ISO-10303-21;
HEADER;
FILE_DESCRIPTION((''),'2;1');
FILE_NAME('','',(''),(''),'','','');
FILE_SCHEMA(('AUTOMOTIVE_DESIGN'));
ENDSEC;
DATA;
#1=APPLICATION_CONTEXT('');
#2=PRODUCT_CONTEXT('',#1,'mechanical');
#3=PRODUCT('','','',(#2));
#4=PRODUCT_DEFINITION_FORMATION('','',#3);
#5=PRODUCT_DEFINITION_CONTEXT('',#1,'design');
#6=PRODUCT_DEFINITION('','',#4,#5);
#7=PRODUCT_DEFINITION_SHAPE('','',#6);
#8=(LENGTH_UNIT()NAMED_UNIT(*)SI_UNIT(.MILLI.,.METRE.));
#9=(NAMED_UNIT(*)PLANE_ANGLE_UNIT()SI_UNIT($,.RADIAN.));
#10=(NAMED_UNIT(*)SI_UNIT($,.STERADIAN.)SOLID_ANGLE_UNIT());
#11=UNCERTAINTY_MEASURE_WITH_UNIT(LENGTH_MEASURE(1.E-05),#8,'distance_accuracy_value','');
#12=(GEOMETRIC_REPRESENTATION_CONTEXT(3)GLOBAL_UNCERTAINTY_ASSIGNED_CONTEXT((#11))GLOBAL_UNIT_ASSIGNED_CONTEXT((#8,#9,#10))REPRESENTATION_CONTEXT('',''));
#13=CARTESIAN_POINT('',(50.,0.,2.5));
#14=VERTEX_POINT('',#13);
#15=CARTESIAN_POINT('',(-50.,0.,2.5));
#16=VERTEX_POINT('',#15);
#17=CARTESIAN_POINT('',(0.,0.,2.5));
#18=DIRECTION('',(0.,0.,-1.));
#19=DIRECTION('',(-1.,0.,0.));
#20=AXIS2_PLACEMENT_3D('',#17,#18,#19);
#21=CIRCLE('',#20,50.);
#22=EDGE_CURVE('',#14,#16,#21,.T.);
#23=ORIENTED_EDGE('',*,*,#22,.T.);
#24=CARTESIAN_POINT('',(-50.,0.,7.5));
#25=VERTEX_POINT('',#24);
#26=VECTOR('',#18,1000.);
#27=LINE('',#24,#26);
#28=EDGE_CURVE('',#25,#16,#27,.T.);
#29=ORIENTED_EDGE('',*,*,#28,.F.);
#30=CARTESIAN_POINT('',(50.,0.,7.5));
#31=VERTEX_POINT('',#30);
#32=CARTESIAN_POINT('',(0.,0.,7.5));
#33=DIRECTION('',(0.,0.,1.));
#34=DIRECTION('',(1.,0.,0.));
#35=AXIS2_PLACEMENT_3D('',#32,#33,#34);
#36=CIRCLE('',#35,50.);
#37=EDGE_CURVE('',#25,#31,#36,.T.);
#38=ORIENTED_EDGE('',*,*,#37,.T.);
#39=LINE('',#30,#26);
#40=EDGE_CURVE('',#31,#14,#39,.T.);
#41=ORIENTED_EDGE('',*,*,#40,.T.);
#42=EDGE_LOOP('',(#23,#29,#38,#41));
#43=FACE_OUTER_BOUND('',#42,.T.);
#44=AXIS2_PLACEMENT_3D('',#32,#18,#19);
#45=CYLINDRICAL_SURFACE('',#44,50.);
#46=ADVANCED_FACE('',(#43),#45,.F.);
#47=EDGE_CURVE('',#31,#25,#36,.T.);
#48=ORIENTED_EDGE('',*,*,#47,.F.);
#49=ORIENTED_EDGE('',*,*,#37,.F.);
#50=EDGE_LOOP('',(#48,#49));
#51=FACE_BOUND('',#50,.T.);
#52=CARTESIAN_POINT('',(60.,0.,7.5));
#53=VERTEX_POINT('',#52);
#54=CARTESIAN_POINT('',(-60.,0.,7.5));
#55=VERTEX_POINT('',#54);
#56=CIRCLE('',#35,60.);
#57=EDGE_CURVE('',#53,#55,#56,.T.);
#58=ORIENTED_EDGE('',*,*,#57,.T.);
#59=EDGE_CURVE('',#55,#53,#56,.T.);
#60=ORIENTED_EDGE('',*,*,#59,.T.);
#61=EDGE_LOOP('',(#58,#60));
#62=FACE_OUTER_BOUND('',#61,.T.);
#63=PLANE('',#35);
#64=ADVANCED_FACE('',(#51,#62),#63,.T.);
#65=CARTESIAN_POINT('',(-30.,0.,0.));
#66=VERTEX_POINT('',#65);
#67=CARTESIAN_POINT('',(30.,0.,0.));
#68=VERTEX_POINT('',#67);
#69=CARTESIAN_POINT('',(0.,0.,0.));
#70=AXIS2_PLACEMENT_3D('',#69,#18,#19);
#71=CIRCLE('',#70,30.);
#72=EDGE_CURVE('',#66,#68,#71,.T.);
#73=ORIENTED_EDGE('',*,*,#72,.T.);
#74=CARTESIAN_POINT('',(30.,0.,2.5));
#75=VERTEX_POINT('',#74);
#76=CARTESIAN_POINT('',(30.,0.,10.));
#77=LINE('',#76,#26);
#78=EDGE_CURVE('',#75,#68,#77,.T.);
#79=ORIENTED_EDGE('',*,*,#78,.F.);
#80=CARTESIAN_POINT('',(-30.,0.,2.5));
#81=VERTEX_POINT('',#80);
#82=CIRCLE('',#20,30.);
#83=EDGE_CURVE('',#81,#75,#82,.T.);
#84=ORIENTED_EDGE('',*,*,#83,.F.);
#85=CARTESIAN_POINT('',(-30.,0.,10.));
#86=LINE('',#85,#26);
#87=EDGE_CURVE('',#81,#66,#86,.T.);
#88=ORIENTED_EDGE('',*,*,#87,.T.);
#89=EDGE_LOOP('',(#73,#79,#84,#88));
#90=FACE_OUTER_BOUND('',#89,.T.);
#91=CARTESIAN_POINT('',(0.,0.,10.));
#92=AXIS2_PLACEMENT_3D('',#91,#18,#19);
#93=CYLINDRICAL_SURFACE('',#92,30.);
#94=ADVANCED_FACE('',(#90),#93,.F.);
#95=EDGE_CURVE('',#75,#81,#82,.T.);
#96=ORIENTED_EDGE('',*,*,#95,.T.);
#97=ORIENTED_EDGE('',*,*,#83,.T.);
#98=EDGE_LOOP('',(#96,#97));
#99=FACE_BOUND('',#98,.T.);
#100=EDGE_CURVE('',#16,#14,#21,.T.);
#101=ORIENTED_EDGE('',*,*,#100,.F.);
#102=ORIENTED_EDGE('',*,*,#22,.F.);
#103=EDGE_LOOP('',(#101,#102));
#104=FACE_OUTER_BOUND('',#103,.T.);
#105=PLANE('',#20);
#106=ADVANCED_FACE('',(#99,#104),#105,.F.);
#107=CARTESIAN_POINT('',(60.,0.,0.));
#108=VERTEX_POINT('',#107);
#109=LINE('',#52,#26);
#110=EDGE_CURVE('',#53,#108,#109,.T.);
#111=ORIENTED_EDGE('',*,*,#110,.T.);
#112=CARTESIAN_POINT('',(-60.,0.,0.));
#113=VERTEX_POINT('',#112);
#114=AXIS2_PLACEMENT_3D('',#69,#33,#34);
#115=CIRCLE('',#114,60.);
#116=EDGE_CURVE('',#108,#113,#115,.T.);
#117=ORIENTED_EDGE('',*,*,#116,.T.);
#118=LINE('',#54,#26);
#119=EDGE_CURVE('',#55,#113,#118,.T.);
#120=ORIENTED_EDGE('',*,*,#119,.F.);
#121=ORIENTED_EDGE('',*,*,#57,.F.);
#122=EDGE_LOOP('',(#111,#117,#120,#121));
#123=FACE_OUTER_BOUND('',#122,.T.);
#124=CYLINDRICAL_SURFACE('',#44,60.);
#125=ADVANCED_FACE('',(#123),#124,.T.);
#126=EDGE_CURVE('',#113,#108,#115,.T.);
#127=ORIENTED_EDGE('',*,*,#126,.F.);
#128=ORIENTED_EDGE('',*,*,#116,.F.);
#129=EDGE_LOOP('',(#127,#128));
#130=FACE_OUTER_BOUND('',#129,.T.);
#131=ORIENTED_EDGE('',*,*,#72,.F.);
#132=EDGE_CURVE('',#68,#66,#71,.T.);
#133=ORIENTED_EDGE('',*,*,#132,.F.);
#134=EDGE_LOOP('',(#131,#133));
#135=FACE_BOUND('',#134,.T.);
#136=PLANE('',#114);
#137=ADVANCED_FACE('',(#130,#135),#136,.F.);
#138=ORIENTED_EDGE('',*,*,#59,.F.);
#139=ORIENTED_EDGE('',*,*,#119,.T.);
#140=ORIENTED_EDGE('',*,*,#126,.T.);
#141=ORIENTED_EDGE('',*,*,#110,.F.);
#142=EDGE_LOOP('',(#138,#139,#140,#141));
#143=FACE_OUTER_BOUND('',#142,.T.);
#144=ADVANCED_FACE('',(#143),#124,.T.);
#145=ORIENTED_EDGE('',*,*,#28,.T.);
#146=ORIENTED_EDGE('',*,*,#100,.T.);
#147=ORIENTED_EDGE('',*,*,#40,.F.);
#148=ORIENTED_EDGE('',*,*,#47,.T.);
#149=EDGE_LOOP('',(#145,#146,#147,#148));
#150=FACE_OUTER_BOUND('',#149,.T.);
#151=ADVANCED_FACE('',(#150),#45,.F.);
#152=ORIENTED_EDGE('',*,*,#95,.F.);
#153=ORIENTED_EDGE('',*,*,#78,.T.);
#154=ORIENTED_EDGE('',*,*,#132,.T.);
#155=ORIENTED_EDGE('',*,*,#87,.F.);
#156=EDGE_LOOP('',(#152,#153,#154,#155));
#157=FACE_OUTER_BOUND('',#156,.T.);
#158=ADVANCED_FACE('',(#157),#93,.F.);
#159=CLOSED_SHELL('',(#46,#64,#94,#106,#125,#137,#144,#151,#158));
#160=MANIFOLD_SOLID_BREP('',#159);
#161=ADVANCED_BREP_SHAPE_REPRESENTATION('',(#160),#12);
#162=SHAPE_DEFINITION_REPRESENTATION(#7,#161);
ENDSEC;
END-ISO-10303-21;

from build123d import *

# Parameters (mm, degrees)
SKETCH_1_R          = 60
SKETCH_1_R_2        = 50
EXTRUDE_1_DEPTH     = 7.5
SKETCH_2_R          = 50
SKETCH_2_R_2        = 20
EXTRUDE_2_DEPTH     = 2.5
SKETCH_4_R          = 30
CUT_EXTRUDE_1_DEPTH = 10


with BuildPart() as part:
    # 草图1 → 拉伸1 (new body)
    with BuildSketch(Plane.XY):
        Circle(SKETCH_1_R)
        Circle(SKETCH_1_R_2, mode=Mode.SUBTRACT)
    extrude(amount=EXTRUDE_1_DEPTH)

    # 草图2 → 拉伸2 (add)
    with BuildSketch(Plane(origin=(0, 0, 0), x_dir=(-1, 0, 0), z_dir=(0, 0, -1))):
        Circle(SKETCH_2_R)
        Circle(SKETCH_2_R_2, mode=Mode.SUBTRACT)
    extrude(amount=-EXTRUDE_2_DEPTH)

    # 草图4 → 切除-拉伸1 (cut)
    with BuildSketch(Plane(origin=(0, 0, 0), x_dir=(-1, 0, 0), z_dir=(0, 0, -1))):
        Circle(SKETCH_4_R)
    extrude(amount=-CUT_EXTRUDE_1_DEPTH, mode=Mode.SUBTRACT)


solid = part.part
